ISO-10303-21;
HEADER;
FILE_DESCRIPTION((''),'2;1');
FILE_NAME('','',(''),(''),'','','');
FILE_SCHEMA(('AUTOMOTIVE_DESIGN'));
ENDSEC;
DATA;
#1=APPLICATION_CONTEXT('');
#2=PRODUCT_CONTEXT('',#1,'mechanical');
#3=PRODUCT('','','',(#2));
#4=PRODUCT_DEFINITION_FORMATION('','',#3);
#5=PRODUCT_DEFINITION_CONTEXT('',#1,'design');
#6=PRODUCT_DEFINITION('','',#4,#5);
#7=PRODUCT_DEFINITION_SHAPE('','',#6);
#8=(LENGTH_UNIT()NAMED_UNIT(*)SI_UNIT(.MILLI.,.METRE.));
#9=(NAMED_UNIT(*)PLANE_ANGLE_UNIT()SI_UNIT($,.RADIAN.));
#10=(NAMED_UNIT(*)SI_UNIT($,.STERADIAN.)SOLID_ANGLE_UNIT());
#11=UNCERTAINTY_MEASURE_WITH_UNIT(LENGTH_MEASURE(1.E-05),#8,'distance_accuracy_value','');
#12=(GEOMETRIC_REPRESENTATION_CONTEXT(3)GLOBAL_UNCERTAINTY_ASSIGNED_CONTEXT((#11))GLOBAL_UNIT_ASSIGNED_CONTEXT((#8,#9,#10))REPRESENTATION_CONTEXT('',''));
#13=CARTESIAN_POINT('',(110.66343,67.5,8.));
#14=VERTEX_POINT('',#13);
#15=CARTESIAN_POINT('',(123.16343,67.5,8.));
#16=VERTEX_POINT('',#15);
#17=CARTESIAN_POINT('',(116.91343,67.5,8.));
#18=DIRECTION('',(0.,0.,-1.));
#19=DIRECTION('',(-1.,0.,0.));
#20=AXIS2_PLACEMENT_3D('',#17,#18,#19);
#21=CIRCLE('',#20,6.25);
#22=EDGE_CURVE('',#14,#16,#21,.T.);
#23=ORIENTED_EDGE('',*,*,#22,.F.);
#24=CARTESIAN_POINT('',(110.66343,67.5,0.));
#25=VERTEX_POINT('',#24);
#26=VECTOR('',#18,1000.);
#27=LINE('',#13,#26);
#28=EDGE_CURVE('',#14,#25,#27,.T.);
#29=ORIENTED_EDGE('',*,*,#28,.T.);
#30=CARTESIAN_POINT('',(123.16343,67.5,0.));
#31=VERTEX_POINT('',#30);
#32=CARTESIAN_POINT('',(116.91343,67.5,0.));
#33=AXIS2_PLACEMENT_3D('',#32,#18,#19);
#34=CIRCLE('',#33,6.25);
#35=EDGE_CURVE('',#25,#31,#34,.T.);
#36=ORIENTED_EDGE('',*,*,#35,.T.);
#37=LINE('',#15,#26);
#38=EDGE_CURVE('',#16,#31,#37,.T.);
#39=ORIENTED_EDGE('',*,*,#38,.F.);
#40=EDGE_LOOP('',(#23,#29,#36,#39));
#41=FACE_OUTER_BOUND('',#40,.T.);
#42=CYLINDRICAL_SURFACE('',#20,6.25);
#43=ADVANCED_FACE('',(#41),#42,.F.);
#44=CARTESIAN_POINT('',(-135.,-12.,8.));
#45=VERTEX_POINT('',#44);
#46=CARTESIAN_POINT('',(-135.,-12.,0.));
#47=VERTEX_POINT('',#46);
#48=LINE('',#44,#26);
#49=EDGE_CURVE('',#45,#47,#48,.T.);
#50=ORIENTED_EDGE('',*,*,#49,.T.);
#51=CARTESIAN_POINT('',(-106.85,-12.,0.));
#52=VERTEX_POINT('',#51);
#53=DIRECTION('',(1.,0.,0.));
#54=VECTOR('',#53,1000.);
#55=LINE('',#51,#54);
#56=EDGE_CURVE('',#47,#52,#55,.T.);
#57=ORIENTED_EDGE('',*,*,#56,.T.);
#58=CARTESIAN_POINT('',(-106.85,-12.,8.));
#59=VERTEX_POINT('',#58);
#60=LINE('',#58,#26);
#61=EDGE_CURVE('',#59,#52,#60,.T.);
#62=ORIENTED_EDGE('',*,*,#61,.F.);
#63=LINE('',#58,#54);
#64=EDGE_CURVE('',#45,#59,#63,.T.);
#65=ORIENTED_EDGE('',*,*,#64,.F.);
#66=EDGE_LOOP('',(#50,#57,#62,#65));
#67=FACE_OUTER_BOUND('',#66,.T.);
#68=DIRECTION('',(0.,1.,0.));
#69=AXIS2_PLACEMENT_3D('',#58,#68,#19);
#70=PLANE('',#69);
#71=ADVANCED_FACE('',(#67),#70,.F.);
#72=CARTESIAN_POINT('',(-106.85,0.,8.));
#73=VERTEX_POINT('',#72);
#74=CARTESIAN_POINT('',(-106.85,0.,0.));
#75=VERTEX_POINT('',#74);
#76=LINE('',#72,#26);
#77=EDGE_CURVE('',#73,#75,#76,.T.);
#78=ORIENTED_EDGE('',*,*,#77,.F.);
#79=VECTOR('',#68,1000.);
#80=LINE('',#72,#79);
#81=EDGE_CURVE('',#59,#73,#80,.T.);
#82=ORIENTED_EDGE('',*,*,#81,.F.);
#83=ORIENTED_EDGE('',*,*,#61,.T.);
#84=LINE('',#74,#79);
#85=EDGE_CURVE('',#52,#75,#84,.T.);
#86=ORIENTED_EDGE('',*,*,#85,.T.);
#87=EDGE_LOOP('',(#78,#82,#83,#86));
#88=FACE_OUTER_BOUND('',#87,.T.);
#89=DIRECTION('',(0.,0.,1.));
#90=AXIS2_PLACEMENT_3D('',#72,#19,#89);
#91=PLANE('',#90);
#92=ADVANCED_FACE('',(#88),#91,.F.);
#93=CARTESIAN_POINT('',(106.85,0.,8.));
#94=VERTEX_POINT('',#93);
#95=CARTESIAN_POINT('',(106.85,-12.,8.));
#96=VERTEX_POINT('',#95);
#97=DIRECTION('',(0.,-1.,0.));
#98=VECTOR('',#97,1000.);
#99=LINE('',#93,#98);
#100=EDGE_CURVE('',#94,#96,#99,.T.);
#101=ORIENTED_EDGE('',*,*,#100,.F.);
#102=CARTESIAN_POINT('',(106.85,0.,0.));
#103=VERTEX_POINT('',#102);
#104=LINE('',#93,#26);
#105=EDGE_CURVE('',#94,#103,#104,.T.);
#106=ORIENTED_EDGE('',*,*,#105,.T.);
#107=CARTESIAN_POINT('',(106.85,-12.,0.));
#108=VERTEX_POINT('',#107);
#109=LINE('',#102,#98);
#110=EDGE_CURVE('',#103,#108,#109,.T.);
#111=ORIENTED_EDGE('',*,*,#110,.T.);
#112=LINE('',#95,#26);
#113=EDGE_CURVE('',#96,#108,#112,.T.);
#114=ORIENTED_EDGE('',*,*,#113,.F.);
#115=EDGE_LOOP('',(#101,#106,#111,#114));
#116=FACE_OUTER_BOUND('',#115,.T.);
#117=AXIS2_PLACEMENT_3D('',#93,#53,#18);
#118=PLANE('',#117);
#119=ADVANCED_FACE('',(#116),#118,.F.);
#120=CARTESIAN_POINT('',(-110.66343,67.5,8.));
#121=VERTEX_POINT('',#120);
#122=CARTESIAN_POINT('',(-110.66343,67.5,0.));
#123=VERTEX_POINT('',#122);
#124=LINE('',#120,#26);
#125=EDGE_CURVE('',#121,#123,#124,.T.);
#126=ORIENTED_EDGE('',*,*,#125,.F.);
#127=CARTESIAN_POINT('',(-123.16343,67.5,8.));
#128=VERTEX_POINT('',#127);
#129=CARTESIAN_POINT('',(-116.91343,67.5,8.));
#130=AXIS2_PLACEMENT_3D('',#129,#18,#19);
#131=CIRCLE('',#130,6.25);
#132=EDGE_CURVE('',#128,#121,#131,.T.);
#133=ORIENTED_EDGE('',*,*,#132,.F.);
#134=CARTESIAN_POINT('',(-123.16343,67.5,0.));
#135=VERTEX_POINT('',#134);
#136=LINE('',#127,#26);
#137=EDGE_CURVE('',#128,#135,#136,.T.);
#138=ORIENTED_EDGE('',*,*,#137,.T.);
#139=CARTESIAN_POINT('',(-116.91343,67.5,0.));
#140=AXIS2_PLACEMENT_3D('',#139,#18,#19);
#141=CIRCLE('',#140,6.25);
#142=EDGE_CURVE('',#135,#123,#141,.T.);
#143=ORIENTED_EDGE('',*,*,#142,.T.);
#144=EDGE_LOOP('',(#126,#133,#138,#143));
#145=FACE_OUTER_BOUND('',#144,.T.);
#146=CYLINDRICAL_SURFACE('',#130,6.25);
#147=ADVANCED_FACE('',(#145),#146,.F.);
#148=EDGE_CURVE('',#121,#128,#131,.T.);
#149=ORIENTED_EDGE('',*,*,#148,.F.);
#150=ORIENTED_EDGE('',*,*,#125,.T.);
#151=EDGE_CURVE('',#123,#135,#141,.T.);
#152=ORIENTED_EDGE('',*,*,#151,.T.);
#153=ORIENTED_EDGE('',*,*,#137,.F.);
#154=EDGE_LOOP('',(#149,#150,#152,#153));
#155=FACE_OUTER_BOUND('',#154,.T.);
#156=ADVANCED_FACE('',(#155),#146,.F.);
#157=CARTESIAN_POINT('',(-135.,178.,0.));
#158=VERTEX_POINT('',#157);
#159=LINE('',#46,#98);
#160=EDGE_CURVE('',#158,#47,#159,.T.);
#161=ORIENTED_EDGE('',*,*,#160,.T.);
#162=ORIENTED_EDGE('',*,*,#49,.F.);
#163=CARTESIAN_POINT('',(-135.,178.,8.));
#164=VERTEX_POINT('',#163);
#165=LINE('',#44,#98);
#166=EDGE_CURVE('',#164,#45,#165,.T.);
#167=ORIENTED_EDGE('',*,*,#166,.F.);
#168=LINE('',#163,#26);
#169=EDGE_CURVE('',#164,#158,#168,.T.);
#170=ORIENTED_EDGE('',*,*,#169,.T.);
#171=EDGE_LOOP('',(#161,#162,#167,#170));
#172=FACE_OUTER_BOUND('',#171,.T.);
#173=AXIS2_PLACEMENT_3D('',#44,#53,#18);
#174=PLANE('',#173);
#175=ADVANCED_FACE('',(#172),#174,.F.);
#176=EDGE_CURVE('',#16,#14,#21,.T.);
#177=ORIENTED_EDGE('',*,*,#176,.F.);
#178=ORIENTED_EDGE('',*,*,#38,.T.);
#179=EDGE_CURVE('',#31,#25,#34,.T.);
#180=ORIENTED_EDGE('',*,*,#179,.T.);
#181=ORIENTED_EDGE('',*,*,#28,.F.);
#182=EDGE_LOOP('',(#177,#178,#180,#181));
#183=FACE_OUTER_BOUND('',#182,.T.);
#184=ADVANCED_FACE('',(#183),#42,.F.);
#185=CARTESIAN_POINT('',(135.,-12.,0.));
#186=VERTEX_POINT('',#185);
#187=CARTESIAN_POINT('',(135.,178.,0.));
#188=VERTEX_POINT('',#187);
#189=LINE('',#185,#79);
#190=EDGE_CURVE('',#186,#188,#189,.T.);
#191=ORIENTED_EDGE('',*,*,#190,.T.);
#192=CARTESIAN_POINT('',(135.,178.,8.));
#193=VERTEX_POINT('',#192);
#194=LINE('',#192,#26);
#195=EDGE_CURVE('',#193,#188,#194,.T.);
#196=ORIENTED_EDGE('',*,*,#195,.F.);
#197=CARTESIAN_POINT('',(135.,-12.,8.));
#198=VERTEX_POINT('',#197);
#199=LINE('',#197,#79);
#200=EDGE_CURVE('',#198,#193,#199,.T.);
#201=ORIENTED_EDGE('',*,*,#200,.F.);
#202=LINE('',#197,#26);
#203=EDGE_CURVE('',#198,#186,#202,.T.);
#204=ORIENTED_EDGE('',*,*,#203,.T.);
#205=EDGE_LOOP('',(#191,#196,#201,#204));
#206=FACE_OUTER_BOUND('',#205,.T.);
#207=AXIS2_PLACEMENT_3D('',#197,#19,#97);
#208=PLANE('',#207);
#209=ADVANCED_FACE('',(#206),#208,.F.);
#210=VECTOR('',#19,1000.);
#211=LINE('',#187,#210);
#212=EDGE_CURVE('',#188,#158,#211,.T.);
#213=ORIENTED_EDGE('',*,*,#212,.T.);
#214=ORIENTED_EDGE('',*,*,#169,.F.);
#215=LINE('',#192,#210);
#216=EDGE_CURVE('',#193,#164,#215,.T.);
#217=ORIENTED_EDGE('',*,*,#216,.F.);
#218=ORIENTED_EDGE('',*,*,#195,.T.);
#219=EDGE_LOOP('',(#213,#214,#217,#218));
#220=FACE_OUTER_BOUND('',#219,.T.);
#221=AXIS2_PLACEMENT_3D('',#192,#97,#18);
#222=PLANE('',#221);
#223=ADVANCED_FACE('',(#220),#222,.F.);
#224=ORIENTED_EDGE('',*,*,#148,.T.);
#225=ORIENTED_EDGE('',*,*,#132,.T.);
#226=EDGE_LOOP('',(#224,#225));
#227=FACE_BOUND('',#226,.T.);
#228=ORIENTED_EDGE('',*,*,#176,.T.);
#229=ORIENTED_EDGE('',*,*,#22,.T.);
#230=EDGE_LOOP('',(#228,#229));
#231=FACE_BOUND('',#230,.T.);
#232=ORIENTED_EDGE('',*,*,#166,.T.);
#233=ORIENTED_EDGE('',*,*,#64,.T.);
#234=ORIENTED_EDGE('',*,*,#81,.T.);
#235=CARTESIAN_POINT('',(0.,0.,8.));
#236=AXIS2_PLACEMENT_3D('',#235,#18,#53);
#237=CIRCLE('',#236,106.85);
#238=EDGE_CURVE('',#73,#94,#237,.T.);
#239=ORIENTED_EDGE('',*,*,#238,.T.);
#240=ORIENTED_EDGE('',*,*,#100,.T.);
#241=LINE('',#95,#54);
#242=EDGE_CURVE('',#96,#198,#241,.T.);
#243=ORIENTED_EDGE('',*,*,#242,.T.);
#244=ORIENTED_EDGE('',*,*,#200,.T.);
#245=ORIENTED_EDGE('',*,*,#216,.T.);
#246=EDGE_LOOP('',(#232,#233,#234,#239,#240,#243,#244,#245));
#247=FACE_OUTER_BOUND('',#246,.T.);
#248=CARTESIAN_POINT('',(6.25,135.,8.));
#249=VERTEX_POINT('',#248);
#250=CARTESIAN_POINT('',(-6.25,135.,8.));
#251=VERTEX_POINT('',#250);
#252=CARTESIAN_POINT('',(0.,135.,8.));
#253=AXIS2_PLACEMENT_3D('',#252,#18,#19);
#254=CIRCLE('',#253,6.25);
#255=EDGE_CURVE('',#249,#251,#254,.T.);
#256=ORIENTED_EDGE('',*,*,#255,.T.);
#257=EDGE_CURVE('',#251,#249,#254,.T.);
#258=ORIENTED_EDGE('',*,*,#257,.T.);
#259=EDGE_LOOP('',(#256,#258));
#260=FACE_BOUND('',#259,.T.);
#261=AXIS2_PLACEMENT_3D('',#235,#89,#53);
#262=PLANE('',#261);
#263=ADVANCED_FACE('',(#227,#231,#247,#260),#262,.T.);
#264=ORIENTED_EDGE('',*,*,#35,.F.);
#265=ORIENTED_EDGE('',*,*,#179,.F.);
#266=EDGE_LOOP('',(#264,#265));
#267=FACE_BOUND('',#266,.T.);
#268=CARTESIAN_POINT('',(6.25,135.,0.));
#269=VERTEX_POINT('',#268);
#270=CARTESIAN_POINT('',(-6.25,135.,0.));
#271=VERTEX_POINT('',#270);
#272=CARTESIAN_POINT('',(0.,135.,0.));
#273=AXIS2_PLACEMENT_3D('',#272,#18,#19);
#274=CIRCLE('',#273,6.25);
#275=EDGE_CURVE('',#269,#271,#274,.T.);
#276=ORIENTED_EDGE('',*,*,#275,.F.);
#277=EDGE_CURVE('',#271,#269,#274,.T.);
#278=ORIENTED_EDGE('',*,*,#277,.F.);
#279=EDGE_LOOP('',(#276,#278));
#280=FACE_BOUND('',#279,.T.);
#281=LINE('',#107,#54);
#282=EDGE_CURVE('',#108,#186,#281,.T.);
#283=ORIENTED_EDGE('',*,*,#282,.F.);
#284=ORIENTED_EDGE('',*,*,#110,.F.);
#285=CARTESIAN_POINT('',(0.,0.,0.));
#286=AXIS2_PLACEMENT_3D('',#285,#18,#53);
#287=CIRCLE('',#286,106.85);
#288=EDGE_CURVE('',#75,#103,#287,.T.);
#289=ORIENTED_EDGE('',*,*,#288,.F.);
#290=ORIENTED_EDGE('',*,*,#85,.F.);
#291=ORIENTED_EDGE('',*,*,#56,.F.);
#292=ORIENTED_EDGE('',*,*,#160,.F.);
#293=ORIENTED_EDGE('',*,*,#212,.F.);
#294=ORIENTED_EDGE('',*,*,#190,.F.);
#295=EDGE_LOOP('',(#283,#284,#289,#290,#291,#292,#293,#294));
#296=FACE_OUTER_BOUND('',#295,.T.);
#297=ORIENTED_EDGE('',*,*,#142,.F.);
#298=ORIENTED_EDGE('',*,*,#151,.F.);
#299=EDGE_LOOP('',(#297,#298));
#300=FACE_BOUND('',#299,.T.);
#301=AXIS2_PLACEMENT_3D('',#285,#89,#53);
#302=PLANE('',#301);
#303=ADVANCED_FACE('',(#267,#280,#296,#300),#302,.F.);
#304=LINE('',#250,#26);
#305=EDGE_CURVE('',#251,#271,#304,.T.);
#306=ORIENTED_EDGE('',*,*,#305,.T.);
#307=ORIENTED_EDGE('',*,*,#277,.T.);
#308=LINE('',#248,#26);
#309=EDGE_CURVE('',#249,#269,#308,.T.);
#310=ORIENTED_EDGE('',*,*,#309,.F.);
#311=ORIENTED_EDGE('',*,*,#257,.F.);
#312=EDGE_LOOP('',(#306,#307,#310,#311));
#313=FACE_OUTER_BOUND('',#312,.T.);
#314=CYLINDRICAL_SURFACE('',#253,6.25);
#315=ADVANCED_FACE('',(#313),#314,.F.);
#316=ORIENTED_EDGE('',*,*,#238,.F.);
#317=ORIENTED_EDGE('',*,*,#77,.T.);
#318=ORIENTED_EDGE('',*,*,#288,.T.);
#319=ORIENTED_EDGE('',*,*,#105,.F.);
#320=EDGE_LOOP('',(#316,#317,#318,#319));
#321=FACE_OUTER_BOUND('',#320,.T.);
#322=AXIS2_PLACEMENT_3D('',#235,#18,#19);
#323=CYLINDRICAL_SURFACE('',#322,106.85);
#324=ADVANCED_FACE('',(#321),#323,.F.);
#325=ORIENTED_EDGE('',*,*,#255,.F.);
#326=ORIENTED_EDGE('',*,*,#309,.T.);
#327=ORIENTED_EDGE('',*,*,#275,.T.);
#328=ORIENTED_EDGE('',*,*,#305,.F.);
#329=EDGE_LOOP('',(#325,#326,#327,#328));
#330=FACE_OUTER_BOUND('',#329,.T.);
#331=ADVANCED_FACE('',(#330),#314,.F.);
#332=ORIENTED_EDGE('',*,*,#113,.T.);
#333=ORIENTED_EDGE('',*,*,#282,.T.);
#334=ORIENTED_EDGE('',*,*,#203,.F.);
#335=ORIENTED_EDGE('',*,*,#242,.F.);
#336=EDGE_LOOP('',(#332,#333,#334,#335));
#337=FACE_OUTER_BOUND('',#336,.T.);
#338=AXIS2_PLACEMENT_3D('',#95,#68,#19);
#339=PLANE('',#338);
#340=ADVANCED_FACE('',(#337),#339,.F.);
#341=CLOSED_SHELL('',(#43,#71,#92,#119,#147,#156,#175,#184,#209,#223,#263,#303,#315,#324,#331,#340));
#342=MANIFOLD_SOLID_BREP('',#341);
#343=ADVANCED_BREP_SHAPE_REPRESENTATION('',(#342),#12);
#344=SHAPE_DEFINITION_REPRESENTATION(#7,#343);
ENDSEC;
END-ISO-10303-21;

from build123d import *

# Parameters (mm, degrees)
BOSS_EXTRUDE1_DEPTH = 8
SKETCH2_R           = 6.25
CUT_EXTRUDE1_DEPTH  = 224.546415762


with BuildPart() as part:
    # Sketch1 → Boss-Extrude1 (new body)
    with BuildSketch(Plane(origin=(0, 0, 0), x_dir=(-1, 0, 0), z_dir=(0, 0, 1))):
        with BuildLine():
            Line((-106.85, 12), (-135, 12))
            Line((-135, 12), (-135, -178))
            Line((-135, -178), (135, -178))
            Line((135, -178), (135, 12))
            Line((135, 12), (106.85, 12))
            Line((106.85, 12), (106.85, 0))
            ThreePointArc((106.85, 0), (0, -106.85), (-106.85, 0))
            Line((-106.85, 0), (-106.85, 12))
        make_face()
    extrude(amount=BOSS_EXTRUDE1_DEPTH)

    # Sketch2 → Cut-Extrude1 (cut, through all)
    with BuildSketch(Plane(origin=(0, 0, 0), x_dir=(-1, 0, 0), z_dir=(0, 0, -1))):
        with Locations((-116.913429511, 67.5)):
            Circle(SKETCH2_R)
        with Locations((116.913429511, 67.5)):
            Circle(SKETCH2_R)
        with Locations((0, 135)):
            Circle(SKETCH2_R)
    extrude(amount=-CUT_EXTRUDE1_DEPTH, mode=Mode.SUBTRACT)


solid = part.part
